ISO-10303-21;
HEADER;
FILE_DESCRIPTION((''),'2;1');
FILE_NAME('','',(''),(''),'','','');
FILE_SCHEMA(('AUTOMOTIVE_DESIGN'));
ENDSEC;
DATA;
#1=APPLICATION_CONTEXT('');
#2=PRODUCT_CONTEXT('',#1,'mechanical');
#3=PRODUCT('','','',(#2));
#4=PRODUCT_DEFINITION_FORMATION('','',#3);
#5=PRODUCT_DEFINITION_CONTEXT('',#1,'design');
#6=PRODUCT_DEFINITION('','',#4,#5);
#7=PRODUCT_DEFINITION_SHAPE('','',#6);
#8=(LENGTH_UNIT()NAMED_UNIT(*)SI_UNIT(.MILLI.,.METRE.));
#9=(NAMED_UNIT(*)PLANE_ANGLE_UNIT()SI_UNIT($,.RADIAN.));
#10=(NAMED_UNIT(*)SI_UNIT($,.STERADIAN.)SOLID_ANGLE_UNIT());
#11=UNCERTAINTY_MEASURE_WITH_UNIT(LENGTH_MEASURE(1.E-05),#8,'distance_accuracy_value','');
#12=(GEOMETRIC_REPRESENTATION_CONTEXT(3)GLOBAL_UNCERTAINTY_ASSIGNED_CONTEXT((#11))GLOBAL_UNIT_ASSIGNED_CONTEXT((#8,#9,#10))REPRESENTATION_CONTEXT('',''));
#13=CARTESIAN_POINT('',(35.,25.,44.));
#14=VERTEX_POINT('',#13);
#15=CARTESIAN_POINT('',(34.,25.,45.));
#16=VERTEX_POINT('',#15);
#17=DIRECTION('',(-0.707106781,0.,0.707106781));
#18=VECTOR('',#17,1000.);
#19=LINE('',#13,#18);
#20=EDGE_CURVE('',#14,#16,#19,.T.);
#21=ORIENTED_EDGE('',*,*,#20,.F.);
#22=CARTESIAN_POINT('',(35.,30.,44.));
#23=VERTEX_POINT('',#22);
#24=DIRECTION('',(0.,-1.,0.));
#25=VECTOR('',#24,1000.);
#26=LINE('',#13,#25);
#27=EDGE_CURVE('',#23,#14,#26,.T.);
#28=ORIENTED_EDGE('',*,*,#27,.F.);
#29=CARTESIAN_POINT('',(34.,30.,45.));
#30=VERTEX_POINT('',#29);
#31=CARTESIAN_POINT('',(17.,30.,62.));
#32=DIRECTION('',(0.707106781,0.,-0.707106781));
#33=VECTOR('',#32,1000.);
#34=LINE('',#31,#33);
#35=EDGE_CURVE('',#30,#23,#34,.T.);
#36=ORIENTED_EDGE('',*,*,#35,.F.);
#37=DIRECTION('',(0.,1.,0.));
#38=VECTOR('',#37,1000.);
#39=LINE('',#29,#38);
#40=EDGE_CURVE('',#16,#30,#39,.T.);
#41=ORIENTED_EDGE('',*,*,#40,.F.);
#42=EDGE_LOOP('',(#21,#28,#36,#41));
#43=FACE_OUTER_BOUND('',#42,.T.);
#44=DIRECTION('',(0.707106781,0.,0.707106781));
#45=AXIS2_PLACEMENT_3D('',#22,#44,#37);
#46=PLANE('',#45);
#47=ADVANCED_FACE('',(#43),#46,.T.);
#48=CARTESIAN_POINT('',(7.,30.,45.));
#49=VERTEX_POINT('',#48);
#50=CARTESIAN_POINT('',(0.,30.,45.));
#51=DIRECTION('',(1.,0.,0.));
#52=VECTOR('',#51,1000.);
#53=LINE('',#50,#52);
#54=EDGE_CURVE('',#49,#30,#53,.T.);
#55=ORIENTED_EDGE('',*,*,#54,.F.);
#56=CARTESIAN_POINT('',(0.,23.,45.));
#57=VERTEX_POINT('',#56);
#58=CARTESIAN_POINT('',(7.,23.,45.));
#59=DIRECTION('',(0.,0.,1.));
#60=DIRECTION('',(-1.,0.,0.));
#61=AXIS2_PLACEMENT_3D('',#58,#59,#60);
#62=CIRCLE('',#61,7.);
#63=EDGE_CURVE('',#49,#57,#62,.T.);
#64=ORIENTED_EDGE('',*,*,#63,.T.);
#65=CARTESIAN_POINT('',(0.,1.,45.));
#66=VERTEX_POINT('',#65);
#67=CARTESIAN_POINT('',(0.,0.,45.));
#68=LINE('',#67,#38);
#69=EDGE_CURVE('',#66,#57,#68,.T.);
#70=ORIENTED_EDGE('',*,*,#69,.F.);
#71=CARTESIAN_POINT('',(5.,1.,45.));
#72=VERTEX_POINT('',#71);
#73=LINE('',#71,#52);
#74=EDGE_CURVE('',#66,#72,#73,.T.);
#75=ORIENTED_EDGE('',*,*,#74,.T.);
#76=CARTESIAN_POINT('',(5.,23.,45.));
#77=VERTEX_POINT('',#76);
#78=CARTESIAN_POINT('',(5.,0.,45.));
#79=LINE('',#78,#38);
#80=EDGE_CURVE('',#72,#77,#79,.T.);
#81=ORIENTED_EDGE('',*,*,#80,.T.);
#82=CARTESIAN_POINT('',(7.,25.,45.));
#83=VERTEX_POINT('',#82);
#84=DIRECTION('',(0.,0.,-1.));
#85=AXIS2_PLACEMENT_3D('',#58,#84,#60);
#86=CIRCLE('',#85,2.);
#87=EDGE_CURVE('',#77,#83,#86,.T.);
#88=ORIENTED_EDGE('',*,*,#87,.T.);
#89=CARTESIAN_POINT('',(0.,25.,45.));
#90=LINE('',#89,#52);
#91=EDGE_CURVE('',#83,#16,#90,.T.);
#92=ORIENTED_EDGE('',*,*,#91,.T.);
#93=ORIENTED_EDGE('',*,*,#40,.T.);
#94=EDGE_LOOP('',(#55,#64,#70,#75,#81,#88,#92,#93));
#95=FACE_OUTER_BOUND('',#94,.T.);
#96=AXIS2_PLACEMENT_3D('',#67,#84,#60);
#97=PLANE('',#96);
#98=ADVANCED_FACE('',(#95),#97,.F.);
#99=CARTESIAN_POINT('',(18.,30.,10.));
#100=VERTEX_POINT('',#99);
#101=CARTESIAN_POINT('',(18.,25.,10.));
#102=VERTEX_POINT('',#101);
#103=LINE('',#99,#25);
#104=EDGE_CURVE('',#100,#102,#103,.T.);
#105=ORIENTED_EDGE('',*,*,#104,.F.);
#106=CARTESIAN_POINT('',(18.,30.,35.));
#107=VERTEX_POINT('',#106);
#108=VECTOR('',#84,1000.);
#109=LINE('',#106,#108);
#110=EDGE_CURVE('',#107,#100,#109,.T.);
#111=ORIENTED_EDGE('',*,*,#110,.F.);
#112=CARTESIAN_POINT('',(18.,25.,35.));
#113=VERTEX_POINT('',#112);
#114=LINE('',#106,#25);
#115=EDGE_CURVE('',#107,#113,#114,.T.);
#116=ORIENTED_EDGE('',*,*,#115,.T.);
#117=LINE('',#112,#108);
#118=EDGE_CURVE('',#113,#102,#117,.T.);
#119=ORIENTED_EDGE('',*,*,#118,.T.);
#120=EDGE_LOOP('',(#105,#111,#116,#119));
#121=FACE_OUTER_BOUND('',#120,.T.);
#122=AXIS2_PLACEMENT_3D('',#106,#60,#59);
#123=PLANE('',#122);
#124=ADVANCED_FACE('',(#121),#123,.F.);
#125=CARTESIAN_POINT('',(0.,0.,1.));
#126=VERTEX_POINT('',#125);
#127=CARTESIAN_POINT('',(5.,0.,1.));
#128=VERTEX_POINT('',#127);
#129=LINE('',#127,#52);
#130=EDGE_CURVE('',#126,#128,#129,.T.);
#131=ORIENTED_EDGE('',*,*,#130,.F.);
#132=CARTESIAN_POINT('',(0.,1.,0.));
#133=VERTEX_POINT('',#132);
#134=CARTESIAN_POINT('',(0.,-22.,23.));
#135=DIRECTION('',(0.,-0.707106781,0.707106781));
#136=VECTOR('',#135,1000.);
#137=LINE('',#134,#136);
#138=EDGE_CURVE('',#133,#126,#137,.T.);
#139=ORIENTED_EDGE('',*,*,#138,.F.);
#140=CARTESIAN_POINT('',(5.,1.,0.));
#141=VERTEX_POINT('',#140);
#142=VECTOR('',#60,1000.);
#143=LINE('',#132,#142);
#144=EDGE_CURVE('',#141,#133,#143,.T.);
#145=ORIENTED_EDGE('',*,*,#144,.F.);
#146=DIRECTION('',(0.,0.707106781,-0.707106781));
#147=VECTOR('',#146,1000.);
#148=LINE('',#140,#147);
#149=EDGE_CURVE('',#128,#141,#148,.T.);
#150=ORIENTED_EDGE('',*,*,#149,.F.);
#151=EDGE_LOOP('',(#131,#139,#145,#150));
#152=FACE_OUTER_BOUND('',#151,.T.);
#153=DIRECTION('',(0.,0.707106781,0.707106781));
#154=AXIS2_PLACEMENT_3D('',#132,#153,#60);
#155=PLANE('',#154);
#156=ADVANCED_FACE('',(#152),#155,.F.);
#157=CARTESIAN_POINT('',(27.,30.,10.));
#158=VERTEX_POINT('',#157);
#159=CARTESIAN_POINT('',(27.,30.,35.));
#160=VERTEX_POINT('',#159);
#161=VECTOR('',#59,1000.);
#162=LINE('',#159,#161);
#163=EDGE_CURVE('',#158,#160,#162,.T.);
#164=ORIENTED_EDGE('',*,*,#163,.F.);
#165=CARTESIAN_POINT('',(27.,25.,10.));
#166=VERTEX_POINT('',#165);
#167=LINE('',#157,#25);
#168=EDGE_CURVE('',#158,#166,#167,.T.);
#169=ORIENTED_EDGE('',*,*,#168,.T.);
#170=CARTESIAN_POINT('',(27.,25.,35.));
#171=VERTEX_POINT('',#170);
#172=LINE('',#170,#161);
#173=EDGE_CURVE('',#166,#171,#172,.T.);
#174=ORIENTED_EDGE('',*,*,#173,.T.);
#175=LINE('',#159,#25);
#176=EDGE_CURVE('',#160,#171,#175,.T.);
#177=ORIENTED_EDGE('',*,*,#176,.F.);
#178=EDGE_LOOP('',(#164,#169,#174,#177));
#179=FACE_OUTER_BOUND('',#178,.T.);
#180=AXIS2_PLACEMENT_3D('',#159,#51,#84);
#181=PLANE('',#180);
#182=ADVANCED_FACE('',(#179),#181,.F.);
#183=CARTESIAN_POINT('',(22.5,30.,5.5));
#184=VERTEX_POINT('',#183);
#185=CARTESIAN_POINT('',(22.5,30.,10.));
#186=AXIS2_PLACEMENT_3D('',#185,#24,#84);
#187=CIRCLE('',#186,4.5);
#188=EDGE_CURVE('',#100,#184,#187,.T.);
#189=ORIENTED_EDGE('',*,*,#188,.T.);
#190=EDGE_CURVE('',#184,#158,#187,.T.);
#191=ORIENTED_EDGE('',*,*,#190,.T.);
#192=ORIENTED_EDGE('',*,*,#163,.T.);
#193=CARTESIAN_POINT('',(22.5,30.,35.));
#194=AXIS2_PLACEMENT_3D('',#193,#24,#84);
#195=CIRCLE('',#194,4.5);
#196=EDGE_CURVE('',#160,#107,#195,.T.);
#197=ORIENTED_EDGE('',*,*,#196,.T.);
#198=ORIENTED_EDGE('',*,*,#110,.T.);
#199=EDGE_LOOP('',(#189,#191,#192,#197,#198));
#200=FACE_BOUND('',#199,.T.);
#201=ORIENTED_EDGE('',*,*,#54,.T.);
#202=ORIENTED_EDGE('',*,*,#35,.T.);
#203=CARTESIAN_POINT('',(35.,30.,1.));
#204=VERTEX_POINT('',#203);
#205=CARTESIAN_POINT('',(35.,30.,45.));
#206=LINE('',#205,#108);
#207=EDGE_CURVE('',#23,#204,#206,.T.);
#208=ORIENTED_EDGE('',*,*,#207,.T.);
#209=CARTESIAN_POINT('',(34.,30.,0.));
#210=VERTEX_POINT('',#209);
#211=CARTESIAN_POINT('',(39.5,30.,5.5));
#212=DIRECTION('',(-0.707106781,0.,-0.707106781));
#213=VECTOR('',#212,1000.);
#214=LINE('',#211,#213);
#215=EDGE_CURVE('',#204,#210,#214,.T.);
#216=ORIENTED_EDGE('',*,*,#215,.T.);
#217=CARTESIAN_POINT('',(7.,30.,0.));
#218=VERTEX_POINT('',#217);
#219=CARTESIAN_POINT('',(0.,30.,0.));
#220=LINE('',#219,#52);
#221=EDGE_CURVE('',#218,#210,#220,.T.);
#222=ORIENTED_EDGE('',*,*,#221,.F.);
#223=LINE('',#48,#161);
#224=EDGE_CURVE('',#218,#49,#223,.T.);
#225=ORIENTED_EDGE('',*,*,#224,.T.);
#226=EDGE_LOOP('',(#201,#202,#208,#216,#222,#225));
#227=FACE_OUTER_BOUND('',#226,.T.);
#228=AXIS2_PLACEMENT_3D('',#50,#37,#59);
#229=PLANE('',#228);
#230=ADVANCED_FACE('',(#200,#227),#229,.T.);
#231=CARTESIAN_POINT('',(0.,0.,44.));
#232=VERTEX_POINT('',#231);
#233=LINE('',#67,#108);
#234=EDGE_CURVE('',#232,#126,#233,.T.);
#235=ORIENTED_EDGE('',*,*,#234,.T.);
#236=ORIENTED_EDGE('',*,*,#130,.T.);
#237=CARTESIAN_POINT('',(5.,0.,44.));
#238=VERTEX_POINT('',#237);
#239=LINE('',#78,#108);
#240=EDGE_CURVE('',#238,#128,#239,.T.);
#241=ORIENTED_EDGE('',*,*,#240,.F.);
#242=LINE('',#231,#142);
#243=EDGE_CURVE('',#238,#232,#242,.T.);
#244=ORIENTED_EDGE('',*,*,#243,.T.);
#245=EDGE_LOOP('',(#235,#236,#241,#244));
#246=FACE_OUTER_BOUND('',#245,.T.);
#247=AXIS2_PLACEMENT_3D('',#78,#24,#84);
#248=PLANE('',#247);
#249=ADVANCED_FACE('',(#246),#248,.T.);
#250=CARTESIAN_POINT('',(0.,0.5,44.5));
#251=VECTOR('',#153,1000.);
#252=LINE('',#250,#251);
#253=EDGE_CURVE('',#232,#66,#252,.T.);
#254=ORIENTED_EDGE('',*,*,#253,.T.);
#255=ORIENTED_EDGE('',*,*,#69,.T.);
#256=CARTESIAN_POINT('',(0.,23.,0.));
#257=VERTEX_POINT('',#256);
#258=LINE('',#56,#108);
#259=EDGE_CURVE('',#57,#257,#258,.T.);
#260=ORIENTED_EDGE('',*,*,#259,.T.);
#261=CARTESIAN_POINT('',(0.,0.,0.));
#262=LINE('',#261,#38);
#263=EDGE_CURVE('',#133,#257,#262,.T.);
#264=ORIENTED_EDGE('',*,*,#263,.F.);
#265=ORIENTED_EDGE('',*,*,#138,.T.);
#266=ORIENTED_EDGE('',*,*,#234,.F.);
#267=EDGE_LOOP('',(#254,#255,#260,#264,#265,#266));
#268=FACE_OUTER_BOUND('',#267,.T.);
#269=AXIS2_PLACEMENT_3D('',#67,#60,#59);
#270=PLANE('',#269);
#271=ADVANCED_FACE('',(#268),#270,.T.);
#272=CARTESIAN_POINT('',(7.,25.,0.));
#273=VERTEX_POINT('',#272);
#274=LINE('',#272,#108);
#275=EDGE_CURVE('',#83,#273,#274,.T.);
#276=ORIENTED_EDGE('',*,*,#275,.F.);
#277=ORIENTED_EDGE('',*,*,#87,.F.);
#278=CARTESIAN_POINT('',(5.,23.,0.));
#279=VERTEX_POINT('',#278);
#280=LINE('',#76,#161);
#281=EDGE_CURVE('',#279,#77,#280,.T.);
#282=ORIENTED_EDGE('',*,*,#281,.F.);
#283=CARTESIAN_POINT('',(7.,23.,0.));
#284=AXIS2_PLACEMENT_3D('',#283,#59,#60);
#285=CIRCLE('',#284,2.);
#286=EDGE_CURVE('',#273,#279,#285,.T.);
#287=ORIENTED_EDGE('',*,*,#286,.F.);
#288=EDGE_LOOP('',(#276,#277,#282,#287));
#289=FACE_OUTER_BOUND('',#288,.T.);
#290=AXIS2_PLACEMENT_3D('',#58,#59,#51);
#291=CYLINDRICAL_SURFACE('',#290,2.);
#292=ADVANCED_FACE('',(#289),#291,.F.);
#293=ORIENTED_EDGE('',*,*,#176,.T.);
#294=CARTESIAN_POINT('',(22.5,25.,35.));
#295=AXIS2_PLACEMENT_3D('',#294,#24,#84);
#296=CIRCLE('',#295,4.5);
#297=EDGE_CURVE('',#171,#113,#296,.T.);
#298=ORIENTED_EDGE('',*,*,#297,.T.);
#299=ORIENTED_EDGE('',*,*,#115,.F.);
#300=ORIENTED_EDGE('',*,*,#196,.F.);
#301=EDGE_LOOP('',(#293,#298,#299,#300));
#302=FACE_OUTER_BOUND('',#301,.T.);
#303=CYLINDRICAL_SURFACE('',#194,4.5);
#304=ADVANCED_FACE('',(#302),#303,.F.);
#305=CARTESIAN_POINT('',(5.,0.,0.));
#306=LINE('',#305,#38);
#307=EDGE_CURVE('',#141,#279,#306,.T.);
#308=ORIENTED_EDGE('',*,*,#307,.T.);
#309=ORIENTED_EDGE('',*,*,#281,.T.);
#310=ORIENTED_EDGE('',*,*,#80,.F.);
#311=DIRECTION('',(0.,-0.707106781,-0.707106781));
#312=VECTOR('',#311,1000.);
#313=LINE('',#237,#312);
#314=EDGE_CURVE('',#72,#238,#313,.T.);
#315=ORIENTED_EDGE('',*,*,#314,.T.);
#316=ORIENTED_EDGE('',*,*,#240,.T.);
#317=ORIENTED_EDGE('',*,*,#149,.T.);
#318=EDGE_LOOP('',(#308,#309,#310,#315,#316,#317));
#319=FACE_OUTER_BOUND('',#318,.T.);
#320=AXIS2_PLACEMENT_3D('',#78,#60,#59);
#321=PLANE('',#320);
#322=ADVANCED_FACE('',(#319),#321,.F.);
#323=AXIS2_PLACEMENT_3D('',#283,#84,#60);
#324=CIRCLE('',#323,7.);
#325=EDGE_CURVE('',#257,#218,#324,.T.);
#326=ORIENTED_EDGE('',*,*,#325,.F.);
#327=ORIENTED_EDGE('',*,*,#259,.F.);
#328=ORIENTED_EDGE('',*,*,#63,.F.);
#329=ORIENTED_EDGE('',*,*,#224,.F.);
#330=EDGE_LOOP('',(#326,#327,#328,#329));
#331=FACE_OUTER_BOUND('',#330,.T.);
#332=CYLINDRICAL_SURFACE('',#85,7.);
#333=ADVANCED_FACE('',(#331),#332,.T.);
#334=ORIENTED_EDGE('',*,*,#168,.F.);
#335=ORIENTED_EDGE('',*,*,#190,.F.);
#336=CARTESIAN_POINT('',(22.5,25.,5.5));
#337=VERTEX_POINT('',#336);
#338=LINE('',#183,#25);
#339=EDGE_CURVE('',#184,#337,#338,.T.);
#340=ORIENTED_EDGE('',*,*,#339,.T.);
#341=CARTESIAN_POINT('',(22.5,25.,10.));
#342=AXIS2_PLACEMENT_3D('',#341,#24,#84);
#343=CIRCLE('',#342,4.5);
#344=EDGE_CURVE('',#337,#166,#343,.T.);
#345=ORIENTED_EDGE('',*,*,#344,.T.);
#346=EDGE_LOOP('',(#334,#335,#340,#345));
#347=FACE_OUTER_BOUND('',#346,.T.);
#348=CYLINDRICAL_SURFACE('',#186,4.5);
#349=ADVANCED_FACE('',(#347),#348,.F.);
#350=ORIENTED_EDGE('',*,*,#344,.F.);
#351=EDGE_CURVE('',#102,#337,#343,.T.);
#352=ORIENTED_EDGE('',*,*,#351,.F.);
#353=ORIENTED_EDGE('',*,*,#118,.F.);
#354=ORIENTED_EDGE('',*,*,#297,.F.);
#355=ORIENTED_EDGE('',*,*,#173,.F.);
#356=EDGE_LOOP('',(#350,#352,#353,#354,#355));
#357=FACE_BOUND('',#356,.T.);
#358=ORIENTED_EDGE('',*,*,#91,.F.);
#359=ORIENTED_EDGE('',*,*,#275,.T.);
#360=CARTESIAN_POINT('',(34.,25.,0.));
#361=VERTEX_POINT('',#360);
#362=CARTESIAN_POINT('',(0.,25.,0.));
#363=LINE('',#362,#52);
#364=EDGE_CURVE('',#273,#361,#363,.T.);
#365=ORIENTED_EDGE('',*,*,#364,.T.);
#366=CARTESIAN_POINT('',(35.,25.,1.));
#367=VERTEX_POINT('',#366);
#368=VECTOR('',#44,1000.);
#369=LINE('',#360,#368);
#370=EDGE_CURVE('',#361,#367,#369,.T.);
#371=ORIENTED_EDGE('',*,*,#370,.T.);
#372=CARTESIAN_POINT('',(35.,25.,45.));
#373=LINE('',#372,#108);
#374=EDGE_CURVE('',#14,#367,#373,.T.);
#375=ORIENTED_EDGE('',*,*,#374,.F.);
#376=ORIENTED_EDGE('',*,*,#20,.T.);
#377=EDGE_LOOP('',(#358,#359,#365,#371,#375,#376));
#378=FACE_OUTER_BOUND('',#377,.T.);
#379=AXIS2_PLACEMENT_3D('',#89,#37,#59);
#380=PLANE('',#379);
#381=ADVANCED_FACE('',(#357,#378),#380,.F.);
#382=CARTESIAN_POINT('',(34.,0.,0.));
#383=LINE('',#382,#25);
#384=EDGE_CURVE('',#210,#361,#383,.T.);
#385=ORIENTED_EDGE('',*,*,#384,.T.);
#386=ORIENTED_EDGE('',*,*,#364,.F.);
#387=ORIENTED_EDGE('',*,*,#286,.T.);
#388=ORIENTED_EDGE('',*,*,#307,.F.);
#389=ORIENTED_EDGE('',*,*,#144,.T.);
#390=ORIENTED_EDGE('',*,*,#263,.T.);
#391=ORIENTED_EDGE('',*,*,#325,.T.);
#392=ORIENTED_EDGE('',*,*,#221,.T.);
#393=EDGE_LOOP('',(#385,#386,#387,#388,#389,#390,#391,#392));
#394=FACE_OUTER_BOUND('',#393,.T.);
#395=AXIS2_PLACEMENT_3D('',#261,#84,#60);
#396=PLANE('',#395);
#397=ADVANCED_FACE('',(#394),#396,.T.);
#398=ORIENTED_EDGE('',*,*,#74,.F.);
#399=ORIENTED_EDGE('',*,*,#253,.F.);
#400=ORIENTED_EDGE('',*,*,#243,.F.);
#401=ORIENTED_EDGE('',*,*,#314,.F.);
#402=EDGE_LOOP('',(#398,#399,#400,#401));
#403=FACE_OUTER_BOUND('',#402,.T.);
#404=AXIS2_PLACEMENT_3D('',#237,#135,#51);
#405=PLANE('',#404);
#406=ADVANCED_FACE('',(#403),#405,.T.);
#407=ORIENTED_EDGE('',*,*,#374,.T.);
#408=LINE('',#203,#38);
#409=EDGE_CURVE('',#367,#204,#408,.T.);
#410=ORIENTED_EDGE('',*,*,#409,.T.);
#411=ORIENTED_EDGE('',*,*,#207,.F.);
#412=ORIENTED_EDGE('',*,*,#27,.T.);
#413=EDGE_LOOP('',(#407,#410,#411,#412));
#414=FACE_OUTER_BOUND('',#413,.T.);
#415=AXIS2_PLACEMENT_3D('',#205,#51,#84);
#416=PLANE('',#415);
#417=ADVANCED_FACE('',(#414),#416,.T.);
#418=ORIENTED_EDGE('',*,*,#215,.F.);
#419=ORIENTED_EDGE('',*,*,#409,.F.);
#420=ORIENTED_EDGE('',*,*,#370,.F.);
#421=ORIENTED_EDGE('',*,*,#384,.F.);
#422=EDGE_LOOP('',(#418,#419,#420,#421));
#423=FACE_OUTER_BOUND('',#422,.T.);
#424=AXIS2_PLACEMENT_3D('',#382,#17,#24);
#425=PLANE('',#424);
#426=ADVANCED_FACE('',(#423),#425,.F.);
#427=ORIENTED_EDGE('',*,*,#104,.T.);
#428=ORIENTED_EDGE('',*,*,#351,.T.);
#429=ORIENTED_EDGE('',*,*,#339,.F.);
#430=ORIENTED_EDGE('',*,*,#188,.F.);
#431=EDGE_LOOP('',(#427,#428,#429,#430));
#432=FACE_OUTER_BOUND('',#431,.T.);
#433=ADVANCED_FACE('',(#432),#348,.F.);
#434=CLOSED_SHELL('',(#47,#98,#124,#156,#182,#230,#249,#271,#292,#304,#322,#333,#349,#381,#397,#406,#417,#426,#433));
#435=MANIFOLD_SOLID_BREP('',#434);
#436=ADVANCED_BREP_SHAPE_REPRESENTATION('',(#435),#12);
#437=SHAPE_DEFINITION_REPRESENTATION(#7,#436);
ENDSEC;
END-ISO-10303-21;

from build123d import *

# Parameters (mm, degrees)
EXTRUDE_1_DEPTH     = 45
CUT_EXTRUDE_1_DEPTH = 63.24949799
FILLET_1_R          = 2
FILLET_2_R          = 7
CHAMFER_1_SIZE      = 1


with BuildPart() as part:
    # 草图1 → 拉伸-薄壁1 (new body)
    with BuildSketch(Plane.XY):
        Polygon((0, 0), (0, 30), (35, 30), (35, 25), (5, 25), (5, 0), align=None)
    extrude(amount=EXTRUDE_1_DEPTH)

    # 草图2 → 切除-拉伸1 (cut, through all)
    with BuildSketch(Plane.XZ.offset(-25)):
        with BuildLine():
            Line((27, 35), (27, 10))
            ThreePointArc((27, 10), (22.5, 5.5), (18, 10))
            Line((18, 10), (18, 35))
            ThreePointArc((18, 35), (22.5, 39.5), (27, 35))
        make_face()
    extrude(amount=-CUT_EXTRUDE_1_DEPTH, mode=Mode.SUBTRACT)

    # 圆角1
    fillet_1_edges = [part.edges().sort_by_distance(p)[0] for p in [
        (5, 25, 22.5),
    ]]
    fillet(fillet_1_edges, radius=FILLET_1_R)

    # 圆角2
    fillet_2_edges = [part.edges().sort_by_distance(p)[0] for p in [
        (0, 30, 22.5),
    ]]
    fillet(fillet_2_edges, radius=FILLET_2_R)

    # 倒角1
    chamfer_1_edges = [part.edges().sort_by_distance(p)[0] for p in [
        (2.5, 0, 45),
        (2.5, 0, 0),
        (35, 27.5, 0),
        (35, 27.5, 45),
    ]]
    chamfer(chamfer_1_edges, length=CHAMFER_1_SIZE)


solid = part.part
